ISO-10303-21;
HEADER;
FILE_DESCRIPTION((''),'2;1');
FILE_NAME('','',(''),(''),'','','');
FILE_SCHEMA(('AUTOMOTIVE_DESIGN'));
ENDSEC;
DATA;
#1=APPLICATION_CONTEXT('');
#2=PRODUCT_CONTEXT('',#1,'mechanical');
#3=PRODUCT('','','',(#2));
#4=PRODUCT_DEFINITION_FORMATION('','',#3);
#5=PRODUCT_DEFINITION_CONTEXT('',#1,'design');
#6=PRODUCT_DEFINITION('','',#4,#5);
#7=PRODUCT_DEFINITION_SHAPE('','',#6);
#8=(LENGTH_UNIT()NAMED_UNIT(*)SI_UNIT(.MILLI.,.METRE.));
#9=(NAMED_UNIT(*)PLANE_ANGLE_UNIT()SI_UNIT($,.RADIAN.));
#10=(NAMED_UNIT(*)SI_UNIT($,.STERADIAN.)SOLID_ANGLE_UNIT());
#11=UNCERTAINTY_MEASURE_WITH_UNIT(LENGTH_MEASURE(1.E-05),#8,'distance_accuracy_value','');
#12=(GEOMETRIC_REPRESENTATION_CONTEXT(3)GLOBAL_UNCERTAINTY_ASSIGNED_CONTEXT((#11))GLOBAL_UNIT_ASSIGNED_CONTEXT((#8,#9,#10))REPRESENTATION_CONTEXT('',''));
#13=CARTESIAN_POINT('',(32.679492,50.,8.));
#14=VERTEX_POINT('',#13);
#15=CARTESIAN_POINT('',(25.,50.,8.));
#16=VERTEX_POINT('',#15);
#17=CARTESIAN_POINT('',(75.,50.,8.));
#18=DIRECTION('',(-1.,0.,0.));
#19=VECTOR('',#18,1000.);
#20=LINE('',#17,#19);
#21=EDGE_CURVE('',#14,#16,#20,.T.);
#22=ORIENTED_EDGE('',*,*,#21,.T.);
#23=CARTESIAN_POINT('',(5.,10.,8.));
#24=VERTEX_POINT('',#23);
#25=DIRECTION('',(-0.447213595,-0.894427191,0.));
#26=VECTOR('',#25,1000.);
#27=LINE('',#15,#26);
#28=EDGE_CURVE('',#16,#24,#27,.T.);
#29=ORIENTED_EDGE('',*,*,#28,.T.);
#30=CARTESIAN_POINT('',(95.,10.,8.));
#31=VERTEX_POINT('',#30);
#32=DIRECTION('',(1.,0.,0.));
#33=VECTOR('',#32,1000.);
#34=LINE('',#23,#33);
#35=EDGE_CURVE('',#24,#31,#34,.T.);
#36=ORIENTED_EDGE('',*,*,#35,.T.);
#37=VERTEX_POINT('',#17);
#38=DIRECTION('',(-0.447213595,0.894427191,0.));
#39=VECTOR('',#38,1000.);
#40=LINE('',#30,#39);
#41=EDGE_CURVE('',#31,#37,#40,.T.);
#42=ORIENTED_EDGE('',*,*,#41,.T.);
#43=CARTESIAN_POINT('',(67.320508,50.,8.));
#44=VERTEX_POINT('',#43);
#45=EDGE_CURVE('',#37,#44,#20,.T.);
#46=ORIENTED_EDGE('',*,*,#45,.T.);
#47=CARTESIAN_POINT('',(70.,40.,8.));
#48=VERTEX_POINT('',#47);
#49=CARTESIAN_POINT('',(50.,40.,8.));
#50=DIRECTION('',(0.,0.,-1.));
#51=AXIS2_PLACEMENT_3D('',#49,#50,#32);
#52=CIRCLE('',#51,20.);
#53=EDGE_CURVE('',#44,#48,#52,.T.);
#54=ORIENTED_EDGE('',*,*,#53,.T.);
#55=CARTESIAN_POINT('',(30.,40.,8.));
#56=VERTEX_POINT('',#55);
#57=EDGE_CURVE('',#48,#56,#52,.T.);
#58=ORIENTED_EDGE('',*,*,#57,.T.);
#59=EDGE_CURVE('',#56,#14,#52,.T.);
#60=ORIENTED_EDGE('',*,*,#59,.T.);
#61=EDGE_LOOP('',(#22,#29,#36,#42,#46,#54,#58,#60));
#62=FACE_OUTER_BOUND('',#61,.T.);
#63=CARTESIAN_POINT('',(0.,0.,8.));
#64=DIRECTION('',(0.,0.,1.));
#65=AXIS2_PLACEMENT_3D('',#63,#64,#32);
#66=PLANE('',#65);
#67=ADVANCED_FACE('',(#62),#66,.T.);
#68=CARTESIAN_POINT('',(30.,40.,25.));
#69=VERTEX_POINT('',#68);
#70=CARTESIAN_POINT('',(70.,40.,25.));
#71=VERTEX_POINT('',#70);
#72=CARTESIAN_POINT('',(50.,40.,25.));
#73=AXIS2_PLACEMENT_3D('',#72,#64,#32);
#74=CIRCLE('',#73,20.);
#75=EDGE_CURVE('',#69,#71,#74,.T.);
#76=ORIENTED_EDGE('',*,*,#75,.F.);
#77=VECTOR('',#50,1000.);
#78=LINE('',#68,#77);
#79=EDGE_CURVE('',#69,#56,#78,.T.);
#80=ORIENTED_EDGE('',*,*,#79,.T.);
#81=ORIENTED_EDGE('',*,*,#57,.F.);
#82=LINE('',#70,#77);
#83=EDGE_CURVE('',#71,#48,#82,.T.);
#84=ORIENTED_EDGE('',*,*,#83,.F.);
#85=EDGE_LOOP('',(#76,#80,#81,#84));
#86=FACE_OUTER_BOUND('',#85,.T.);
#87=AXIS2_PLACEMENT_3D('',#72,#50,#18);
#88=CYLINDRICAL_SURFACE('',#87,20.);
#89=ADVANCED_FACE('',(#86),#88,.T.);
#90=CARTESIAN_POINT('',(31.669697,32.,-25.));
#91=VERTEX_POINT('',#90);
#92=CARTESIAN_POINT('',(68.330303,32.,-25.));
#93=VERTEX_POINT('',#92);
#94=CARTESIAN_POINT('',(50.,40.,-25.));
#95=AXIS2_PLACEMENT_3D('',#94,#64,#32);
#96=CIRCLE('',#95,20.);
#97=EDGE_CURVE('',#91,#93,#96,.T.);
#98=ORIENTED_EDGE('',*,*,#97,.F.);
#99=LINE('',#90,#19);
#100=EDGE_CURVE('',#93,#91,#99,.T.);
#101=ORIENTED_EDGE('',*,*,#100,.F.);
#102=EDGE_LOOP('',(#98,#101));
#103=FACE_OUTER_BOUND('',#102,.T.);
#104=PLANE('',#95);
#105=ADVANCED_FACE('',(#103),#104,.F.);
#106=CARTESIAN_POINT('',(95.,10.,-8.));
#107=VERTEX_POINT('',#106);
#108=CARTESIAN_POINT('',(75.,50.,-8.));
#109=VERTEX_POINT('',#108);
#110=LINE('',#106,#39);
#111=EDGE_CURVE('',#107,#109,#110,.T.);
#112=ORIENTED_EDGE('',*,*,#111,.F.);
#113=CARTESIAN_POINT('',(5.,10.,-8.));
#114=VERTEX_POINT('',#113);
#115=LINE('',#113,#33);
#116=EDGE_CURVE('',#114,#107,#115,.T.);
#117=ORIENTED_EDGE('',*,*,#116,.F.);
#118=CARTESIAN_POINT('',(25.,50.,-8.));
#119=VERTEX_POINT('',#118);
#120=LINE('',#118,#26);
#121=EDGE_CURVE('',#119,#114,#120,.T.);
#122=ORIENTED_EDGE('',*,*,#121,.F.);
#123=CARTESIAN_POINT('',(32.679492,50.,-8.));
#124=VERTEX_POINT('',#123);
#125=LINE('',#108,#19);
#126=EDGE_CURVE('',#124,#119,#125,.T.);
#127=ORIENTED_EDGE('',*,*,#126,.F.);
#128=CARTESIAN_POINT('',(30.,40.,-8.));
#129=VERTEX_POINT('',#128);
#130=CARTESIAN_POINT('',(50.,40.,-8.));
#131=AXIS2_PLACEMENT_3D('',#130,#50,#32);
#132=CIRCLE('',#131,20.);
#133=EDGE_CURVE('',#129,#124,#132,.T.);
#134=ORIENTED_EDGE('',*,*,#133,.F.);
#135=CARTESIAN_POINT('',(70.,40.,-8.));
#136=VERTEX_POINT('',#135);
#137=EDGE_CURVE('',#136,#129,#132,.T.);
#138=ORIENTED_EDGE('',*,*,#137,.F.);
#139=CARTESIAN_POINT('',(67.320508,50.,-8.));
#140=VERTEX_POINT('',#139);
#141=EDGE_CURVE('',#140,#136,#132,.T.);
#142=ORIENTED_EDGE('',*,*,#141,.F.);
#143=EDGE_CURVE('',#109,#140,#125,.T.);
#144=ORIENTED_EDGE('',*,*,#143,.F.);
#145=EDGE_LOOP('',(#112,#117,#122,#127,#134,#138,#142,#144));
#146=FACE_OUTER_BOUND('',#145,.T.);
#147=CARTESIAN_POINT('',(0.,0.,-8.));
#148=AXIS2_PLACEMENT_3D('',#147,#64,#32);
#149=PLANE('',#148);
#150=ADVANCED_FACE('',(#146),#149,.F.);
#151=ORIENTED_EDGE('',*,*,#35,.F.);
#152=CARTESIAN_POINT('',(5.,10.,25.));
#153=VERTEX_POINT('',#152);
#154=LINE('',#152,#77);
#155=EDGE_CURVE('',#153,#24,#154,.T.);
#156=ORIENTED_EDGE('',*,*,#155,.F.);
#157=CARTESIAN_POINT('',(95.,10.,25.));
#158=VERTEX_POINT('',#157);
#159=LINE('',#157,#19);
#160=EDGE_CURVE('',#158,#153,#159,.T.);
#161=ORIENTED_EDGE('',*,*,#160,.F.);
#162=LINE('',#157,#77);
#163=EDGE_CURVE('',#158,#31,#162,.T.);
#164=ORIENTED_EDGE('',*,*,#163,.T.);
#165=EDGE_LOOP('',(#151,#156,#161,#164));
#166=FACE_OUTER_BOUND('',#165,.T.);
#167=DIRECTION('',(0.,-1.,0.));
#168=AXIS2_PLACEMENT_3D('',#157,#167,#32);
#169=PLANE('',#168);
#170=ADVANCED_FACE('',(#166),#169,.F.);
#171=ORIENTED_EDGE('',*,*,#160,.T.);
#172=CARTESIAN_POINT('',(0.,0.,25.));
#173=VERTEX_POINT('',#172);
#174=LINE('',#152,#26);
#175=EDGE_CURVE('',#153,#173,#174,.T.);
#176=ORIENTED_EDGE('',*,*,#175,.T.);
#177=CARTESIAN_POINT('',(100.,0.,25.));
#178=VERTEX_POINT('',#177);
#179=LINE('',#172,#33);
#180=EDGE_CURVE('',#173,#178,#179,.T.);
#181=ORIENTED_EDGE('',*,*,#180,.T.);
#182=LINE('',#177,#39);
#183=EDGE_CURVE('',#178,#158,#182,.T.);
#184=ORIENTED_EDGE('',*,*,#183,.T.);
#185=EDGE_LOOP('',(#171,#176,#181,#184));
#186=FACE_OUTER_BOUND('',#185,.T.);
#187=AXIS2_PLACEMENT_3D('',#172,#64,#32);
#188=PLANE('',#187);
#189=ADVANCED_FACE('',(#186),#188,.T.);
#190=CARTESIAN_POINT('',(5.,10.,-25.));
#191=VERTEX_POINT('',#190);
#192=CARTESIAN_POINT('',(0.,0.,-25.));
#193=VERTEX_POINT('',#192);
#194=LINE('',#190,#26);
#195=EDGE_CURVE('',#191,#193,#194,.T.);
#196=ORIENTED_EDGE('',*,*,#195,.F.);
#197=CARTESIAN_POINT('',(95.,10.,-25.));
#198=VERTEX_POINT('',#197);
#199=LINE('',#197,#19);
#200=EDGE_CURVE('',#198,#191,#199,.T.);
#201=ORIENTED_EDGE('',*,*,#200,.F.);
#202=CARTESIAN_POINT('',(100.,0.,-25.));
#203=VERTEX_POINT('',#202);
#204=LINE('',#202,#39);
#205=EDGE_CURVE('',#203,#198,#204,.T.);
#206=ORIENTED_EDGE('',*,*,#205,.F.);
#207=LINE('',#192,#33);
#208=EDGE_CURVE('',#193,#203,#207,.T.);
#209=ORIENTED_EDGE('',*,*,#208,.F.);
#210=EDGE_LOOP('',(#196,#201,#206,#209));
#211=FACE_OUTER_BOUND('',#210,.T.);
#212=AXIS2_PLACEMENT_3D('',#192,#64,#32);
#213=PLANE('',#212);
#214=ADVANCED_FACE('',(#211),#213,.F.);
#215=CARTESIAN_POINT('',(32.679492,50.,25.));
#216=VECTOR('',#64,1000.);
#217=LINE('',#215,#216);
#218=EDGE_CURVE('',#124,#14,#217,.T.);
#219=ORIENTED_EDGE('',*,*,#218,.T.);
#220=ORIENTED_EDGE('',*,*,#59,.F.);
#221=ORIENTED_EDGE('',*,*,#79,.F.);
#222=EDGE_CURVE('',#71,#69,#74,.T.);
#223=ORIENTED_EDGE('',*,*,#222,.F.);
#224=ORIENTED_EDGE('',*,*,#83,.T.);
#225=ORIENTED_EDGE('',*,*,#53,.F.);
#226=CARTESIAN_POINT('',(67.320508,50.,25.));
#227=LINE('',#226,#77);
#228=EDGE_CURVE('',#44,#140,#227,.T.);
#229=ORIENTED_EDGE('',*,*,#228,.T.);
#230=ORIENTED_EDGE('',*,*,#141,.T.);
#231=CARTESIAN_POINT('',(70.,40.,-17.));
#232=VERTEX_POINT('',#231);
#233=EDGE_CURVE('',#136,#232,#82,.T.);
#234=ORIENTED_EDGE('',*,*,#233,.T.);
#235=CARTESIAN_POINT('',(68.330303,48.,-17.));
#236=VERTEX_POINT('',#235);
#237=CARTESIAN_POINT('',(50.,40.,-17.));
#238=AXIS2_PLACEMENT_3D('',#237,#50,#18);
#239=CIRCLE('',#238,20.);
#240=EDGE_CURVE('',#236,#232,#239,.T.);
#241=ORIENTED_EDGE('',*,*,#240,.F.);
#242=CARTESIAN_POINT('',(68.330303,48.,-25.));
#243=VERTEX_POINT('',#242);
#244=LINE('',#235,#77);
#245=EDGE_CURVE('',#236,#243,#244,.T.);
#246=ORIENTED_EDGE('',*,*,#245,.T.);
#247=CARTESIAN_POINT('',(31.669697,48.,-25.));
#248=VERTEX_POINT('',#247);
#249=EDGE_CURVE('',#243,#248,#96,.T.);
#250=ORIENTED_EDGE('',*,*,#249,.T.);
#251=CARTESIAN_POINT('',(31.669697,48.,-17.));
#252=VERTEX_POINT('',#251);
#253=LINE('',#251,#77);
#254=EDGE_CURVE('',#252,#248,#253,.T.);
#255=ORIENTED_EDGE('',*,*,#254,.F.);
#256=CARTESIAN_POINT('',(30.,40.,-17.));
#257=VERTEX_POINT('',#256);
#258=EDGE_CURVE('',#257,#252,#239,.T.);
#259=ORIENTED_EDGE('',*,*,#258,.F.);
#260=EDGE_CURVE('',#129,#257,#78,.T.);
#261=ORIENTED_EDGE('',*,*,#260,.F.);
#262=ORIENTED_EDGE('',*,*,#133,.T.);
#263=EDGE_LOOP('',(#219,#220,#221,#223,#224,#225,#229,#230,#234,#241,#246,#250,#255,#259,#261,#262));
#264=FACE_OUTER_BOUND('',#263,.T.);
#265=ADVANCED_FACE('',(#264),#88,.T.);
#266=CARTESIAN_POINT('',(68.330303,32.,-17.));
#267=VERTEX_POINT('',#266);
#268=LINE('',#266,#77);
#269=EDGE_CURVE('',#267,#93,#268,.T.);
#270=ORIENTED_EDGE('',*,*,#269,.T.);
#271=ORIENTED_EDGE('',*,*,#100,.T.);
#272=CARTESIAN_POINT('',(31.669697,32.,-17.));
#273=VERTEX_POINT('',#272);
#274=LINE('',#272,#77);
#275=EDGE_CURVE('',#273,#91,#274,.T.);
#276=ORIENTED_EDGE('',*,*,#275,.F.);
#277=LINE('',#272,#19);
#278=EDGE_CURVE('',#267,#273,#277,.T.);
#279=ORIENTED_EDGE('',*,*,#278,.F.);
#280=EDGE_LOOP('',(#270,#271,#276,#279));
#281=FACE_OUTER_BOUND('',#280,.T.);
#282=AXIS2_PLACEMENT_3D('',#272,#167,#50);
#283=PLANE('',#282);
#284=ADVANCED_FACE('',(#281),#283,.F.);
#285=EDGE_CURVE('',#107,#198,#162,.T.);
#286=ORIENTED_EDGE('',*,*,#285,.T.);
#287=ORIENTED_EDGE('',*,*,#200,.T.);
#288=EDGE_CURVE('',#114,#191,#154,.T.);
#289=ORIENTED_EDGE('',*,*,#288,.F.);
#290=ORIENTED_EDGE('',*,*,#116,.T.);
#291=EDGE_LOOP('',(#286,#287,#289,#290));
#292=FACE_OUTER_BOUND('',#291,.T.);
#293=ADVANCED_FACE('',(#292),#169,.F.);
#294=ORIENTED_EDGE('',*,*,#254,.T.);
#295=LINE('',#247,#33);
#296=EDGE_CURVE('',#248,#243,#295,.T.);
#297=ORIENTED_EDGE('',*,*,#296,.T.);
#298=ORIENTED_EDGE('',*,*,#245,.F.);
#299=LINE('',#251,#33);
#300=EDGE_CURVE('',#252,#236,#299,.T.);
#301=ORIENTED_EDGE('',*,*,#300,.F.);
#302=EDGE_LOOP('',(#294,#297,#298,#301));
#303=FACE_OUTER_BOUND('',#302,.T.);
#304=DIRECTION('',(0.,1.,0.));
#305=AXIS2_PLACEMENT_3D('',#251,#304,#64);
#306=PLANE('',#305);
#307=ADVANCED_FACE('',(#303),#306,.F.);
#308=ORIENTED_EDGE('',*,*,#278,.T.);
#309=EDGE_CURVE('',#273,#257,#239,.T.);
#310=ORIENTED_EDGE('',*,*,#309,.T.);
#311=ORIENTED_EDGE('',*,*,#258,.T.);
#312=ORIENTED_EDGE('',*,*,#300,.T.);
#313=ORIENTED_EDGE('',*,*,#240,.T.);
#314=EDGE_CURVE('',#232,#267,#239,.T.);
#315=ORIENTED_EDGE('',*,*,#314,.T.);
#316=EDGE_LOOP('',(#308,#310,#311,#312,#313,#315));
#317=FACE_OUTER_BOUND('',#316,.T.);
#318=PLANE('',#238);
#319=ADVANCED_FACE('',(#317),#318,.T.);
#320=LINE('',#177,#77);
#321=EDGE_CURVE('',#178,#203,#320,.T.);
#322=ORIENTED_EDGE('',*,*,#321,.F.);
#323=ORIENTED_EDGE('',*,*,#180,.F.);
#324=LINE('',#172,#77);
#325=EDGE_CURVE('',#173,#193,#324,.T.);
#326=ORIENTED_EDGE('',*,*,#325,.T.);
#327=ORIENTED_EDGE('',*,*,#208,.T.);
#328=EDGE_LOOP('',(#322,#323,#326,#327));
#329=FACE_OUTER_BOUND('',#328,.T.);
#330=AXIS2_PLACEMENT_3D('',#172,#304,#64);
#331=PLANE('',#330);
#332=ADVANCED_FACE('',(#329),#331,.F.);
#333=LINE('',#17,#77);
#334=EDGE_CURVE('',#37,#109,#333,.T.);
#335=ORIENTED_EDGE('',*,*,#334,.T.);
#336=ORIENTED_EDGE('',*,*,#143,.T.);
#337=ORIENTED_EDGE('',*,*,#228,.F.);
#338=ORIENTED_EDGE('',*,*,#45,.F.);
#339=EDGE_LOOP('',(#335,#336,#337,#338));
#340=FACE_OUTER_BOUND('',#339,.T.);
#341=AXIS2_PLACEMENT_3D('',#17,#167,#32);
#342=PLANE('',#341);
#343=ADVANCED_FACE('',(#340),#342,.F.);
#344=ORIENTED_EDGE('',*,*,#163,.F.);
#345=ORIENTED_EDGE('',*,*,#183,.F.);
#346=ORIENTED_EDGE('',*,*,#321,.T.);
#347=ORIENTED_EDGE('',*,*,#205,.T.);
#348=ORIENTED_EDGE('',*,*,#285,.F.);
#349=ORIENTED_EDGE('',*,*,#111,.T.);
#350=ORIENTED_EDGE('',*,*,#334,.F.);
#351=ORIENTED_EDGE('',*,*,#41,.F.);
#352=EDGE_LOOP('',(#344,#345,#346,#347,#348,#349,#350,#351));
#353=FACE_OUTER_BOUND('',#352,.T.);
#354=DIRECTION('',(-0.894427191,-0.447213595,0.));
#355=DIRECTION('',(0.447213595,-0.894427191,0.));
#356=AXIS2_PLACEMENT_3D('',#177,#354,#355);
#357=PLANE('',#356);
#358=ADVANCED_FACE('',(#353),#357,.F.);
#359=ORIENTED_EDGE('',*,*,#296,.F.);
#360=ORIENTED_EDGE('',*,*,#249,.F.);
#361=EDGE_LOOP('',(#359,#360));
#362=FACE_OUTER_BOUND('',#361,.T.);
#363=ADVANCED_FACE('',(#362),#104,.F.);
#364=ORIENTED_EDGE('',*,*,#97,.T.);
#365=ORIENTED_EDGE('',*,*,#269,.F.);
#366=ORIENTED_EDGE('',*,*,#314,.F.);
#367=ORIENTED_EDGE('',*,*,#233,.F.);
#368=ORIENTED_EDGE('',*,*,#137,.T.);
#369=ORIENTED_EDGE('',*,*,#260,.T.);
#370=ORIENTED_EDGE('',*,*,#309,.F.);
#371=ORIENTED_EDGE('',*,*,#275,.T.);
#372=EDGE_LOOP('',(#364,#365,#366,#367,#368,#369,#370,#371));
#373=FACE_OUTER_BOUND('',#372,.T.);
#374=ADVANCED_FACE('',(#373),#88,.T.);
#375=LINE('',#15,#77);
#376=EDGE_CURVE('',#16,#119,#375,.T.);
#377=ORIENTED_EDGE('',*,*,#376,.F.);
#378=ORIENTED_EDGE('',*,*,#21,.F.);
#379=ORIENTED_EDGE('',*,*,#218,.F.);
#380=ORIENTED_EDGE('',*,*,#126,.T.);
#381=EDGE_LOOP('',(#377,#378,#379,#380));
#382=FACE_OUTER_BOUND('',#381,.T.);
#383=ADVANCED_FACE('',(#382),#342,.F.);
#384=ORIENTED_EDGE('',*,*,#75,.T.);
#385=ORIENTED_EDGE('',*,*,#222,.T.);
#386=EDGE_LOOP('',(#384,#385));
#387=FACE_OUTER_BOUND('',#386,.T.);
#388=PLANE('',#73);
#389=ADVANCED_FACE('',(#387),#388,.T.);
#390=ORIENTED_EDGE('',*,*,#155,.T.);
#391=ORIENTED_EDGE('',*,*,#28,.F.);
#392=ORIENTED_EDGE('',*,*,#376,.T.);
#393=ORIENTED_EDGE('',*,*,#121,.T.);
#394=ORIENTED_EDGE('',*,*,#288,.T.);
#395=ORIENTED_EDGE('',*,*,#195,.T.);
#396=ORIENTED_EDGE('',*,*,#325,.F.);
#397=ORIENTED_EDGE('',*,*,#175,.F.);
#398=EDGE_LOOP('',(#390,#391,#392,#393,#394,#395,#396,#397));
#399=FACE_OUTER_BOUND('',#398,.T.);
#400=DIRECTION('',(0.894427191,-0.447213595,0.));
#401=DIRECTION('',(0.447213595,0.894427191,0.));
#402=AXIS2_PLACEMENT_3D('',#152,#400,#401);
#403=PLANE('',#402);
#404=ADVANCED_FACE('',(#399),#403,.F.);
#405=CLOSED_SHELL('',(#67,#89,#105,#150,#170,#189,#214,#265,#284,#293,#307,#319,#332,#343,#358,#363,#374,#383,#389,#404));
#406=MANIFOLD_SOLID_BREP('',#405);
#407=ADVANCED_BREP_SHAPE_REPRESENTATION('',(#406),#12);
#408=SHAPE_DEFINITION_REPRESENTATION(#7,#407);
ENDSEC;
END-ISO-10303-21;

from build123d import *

# Parameters (mm, degrees)
BASE_PLATE_DEPTH        = 25
SUPPORT_UPRIGHT_DEPTH   = 8
SHAFT_CYLINDER_SKETCH_R = 20
SHAFT_CYLINDER_40_DEPTH = 25
SHAFT_START             = -8
SHAFT_END_NOTCH_DEPTH   = 8


with BuildPart() as part:
    # Base Plate Sketch → Base Plate (new, symmetric)
    with BuildSketch(Plane.XY):
        Polygon((0, 0), (100, 0), (95, 10), (5, 10), align=None)
    extrude(amount=BASE_PLATE_DEPTH, both=True)

    # Support Upright Sketch → Support Upright (add, symmetric)
    with BuildSketch(Plane.XY):
        Polygon((5, 10), (95, 10), (75, 50), (25, 50), align=None)
    extrude(amount=SUPPORT_UPRIGHT_DEPTH, both=True)

    # Shaft Cylinder Sketch → Shaft Cylinder Ø40 (add, symmetric)
    with BuildSketch(Plane.XY):
        with Locations((50, 40)):
            Circle(SHAFT_CYLINDER_SKETCH_R)
    extrude(amount=SHAFT_CYLINDER_40_DEPTH, both=True)

    # Shaft End Notch Sketch → Shaft End Notch (cut)
    with BuildSketch(Plane(origin=(0, 0, -25), x_dir=(-1, 0, 0), z_dir=(0, 0, -1)).offset(SHAFT_START)):
        with BuildLine():
            Line((-31.66969722, 48), (-68.33030278, 48))
            ThreePointArc((-68.33030278, 48), (-70, 40), (-68.33030278, 32))
            Line((-68.33030278, 32), (-31.66969722, 32))
            ThreePointArc((-31.66969722, 32), (-30, 40), (-31.66969722, 48))
        make_face()
    extrude(amount=SHAFT_END_NOTCH_DEPTH, mode=Mode.SUBTRACT)


solid = part.part
